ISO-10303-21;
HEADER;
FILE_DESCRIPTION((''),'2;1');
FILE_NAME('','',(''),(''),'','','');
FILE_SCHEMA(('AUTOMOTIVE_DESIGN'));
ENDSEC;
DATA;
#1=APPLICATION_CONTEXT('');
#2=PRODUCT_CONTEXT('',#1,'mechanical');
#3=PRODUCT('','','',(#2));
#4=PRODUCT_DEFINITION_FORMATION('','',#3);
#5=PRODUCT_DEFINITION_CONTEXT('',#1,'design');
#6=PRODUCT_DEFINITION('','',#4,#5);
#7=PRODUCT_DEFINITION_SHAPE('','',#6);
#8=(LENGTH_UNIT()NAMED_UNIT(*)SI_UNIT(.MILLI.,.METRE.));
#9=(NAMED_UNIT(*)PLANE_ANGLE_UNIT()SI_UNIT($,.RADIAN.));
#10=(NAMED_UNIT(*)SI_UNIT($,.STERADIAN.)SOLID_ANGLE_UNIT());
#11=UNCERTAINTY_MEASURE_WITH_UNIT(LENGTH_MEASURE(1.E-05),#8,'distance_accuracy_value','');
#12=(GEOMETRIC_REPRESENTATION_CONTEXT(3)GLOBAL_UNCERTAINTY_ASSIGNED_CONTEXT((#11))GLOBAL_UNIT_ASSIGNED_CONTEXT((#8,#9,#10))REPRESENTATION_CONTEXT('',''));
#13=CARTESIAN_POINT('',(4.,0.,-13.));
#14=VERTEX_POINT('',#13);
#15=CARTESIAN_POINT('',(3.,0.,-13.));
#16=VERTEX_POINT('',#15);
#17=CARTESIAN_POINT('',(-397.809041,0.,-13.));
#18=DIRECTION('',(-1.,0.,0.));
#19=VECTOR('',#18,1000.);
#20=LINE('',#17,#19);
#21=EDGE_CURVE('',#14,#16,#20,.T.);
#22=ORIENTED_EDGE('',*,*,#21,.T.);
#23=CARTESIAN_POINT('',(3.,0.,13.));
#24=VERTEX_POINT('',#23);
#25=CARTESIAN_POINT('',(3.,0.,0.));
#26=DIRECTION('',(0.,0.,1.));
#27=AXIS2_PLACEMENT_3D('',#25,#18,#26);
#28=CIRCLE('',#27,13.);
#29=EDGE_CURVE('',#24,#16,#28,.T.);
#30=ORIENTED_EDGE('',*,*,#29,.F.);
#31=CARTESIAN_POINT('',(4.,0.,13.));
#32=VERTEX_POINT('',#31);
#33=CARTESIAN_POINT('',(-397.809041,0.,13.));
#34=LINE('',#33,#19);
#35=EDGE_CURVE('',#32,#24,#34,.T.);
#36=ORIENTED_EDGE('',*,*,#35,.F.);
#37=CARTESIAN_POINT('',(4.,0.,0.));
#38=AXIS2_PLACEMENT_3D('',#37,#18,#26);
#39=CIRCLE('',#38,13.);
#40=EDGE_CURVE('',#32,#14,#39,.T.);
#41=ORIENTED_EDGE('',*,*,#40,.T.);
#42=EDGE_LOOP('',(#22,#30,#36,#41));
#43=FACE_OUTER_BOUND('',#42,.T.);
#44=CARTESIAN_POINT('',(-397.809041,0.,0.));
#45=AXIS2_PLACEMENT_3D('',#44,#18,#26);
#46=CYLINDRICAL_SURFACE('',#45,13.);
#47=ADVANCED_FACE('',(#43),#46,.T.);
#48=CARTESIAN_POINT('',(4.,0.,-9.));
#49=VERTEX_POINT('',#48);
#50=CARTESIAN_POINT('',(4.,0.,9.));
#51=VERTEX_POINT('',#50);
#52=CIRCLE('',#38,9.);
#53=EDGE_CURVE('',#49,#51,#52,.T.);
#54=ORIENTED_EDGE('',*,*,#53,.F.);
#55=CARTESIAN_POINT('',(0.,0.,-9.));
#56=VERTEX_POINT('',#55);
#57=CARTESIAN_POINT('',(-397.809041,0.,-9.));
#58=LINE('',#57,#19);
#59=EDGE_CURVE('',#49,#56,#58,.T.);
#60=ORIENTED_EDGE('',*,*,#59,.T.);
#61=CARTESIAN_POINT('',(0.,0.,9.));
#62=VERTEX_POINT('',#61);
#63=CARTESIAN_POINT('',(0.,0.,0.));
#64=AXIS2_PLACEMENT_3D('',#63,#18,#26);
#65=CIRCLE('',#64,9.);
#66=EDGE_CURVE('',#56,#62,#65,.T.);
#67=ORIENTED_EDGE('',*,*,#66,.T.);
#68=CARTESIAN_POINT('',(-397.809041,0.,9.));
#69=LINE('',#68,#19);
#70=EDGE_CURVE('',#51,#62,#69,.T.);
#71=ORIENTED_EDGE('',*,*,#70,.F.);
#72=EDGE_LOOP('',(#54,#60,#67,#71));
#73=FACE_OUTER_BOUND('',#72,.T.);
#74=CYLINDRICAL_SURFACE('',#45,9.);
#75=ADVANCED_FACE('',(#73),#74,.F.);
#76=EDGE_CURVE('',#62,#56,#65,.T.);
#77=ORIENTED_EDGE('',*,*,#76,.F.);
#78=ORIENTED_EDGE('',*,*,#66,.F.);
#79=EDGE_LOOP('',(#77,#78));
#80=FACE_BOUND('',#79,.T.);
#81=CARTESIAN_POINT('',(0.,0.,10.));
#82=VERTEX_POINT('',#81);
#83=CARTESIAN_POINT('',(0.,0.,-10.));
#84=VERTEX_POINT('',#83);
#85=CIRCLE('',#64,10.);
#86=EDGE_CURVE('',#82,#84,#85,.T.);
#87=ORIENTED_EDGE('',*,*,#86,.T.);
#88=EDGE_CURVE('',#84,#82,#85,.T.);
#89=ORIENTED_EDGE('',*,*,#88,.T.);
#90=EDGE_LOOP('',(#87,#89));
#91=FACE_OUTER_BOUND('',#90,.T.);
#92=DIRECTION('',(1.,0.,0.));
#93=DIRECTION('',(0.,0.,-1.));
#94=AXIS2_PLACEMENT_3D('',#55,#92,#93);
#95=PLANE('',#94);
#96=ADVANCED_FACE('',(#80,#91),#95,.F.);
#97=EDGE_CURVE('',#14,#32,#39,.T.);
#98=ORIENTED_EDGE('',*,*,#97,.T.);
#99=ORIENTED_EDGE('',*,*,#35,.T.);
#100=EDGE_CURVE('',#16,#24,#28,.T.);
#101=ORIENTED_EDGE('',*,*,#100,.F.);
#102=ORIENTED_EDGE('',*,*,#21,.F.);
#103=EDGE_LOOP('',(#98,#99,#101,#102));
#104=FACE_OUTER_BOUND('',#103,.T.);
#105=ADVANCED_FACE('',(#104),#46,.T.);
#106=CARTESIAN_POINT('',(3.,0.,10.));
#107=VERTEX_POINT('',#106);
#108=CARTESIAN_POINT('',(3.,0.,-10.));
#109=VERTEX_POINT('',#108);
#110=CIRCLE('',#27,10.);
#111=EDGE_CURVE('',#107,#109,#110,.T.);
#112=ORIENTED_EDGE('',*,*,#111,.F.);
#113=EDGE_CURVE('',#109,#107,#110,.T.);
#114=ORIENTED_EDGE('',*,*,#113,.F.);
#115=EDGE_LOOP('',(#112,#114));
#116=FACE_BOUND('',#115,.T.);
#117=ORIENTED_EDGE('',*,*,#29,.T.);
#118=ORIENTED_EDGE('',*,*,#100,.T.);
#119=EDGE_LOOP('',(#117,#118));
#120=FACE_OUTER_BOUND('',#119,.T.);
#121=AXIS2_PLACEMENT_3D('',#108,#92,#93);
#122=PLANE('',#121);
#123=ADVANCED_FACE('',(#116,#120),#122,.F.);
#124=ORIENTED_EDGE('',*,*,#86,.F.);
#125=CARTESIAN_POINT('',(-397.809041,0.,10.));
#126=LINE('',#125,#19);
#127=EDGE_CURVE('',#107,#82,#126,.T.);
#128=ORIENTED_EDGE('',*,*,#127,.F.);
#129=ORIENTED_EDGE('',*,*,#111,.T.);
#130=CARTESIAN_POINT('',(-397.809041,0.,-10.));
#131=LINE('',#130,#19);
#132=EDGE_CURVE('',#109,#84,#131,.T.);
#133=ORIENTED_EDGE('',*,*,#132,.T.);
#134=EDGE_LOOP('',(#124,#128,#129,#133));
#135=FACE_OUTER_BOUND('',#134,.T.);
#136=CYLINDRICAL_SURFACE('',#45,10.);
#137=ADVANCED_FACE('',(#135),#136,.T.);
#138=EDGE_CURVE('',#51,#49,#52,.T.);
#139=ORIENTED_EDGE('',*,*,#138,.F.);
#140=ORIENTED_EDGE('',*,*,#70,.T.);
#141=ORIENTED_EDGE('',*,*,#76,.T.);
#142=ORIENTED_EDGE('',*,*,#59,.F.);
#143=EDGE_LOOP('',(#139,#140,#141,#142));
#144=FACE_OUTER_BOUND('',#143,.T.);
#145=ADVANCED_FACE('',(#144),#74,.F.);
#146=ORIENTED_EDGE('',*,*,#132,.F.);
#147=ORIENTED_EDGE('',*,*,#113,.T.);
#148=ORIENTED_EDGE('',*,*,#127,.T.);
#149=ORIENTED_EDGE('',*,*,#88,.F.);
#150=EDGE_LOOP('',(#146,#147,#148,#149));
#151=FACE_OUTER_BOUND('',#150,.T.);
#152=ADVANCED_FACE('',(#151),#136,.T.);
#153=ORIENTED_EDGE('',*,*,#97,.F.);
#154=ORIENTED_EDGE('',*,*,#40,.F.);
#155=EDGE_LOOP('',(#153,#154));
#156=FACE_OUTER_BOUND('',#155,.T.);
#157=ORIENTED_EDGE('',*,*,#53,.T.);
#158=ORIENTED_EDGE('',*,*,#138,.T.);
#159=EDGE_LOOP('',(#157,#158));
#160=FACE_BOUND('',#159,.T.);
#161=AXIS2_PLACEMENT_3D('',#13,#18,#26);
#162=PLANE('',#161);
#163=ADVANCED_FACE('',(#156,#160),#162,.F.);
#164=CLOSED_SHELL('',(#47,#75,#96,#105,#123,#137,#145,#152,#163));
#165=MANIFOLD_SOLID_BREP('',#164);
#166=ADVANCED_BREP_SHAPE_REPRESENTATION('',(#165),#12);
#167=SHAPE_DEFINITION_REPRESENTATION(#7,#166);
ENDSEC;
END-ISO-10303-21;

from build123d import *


with BuildPart() as part:
    # 草图1 → 旋转1 (revolve)
    with BuildSketch(Plane(origin=(0, 0, 0), x_dir=(1, 0, 0), z_dir=(0, 1, 0)), mode=Mode.PRIVATE) as revolve_1_sk:
        Polygon((0, 9), (0, 10), (3, 10), (3, 13), (4, 13), (4, 9), align=None)
    revolve(revolve_1_sk.sketch.rotate(Axis((-397.809040607, 0, 0), (1, 0, 0)), 180), axis=Axis((-397.809040607, 0, 0), (1, 0, 0)))


solid = part.part
